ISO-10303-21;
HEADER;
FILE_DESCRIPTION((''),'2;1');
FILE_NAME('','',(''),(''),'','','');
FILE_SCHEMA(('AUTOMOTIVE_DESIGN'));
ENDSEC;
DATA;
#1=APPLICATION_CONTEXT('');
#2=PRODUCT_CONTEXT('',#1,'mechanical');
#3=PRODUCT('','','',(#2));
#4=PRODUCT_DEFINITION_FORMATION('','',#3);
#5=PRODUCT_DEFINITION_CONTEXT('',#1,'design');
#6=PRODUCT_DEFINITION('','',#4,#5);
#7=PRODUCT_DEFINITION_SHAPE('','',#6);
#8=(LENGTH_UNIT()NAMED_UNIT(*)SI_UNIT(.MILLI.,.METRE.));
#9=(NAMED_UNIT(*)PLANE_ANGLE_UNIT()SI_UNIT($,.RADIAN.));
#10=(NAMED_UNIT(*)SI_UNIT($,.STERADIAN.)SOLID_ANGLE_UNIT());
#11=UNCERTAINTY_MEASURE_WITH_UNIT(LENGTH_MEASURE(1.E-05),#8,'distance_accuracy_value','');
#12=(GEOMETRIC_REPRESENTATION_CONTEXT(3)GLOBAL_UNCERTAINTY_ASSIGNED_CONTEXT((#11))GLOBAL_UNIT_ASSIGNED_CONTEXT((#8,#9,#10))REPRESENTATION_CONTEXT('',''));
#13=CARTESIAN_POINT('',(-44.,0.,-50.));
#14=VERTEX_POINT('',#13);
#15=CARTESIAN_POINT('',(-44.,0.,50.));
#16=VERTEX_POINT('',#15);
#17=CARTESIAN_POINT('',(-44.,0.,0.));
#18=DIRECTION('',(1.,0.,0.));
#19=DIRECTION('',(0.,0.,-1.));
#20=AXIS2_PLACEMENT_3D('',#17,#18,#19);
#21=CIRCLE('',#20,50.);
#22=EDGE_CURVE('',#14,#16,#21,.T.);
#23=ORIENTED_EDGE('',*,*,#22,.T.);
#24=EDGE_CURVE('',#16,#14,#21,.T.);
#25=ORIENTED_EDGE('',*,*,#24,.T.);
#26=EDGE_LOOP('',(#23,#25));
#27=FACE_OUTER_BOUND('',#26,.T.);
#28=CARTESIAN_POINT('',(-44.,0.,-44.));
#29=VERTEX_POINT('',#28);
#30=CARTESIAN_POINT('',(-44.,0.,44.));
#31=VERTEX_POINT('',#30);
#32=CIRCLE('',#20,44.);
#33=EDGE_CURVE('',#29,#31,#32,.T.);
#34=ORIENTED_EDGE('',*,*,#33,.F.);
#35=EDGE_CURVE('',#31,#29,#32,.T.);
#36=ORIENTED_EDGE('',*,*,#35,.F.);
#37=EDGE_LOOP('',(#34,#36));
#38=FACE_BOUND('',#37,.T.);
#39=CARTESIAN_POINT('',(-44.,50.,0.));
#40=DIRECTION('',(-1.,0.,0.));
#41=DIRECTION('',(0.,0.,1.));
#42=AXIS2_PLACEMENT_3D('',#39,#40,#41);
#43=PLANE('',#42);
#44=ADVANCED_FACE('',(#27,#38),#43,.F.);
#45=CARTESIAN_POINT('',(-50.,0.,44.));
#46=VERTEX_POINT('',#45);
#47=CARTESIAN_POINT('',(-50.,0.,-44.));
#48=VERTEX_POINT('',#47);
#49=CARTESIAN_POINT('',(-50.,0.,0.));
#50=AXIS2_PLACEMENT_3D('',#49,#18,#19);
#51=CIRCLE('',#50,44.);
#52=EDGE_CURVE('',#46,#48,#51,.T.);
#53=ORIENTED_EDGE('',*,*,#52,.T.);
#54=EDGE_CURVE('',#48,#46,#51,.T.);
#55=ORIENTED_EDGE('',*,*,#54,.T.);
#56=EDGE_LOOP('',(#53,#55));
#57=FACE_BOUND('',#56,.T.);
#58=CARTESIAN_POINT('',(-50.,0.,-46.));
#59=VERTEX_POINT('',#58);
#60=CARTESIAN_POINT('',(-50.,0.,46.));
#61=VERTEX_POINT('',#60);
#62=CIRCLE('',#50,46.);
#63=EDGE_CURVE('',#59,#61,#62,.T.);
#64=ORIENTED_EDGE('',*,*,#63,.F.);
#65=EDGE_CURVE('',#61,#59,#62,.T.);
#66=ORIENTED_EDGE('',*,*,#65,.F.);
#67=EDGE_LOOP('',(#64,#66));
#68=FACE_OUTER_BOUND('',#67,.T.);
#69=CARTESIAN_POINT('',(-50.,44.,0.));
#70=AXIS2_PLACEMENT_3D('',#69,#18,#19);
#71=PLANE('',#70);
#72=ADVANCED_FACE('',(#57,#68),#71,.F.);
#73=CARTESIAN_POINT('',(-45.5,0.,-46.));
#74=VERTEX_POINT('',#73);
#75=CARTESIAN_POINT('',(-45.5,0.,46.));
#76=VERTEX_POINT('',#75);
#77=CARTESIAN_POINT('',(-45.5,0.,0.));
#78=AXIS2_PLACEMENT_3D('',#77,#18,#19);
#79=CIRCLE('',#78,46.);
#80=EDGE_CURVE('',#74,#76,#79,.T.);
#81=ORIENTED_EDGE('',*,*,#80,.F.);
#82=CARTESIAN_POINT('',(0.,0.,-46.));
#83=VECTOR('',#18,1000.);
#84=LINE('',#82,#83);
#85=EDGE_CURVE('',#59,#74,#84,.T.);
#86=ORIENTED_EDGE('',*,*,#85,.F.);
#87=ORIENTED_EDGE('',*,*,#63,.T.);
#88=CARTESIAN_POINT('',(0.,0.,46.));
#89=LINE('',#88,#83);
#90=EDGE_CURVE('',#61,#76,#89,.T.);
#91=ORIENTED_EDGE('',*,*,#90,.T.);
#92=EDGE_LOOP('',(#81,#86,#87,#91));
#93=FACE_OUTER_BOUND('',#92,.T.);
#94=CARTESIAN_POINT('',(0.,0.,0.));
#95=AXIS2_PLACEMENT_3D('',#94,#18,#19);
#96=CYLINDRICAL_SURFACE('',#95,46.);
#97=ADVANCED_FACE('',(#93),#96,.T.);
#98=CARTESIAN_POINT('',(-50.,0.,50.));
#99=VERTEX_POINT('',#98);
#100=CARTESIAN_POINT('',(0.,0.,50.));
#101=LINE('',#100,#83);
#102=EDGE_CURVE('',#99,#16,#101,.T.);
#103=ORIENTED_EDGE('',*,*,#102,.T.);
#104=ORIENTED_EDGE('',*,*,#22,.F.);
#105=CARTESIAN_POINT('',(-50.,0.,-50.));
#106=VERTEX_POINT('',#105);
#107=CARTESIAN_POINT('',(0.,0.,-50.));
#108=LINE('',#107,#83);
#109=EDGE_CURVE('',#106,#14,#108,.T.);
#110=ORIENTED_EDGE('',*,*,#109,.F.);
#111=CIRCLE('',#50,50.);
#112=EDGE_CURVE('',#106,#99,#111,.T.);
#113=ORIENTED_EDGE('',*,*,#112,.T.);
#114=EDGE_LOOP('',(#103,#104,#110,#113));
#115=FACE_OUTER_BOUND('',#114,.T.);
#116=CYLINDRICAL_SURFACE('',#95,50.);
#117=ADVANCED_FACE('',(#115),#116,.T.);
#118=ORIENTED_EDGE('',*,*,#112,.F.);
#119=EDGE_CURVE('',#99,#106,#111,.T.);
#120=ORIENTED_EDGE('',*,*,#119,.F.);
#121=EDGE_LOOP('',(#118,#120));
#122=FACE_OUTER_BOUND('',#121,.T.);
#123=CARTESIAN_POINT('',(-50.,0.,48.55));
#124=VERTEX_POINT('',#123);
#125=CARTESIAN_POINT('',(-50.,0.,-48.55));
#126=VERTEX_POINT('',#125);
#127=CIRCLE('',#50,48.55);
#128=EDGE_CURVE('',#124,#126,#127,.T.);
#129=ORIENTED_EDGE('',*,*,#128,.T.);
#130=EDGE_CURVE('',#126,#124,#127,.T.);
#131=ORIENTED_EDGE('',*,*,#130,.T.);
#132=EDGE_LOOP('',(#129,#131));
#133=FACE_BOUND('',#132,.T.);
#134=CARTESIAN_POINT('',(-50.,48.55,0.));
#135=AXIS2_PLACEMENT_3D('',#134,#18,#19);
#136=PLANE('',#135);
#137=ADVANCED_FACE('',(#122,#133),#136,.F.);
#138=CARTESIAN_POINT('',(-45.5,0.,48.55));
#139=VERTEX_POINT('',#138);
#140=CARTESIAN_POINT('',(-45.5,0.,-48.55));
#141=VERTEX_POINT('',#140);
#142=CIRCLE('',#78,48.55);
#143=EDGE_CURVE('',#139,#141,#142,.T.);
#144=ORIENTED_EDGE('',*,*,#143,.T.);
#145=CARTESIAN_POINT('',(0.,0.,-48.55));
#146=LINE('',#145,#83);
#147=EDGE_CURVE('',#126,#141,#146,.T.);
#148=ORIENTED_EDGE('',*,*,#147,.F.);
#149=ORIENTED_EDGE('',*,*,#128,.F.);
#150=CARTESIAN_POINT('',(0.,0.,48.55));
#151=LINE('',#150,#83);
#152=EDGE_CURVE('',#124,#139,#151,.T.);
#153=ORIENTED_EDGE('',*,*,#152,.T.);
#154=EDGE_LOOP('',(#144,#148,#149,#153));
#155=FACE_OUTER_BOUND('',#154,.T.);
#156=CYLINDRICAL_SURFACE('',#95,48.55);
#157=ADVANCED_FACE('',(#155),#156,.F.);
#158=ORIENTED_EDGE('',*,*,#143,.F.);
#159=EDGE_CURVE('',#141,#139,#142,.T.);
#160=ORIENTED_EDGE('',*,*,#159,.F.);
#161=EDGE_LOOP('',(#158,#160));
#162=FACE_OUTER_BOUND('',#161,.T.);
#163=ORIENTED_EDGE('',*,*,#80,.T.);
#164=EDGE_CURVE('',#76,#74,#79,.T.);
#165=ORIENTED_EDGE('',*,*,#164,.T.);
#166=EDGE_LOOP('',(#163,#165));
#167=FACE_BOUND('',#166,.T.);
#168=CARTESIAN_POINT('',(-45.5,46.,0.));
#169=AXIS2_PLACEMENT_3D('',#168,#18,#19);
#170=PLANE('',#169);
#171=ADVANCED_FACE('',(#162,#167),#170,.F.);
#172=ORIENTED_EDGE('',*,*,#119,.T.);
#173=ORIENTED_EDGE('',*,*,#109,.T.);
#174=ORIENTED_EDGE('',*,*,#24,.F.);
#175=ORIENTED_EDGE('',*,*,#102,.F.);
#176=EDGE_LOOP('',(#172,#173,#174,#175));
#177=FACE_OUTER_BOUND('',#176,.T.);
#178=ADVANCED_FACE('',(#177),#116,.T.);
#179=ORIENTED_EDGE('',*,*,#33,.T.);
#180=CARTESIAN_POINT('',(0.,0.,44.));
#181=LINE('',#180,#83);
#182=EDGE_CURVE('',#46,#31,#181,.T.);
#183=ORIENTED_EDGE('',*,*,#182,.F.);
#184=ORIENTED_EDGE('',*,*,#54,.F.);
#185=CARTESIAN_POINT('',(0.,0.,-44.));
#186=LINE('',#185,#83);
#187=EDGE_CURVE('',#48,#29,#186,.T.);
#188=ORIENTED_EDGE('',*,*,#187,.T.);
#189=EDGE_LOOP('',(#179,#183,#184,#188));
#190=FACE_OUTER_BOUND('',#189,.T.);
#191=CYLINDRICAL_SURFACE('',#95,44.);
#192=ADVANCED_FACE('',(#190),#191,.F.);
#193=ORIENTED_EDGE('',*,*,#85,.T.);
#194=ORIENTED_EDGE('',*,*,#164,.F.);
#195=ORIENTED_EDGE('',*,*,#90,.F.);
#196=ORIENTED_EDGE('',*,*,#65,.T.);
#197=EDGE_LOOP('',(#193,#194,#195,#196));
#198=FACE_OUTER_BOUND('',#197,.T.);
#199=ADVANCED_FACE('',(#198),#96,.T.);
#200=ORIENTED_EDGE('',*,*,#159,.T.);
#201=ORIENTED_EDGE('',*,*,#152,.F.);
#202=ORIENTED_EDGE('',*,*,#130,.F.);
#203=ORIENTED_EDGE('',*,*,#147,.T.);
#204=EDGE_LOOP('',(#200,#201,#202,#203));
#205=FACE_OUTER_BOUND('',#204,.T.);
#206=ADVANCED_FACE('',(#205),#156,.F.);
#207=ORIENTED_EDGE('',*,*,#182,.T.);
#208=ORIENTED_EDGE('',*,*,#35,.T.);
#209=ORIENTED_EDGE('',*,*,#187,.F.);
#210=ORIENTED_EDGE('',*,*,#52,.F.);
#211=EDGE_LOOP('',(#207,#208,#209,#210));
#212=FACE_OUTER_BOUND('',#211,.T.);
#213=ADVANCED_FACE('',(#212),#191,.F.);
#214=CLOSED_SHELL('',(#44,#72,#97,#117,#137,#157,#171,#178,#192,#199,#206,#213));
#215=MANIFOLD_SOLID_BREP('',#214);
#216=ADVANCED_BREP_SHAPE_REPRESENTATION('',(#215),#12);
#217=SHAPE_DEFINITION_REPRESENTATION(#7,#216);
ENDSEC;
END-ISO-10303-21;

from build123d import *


with BuildPart() as part:
    # Sketch1 → Revolve1 (revolve)
    with BuildSketch(Plane.XY, mode=Mode.PRIVATE) as revolve1_sk:
        Polygon((-50, 48.55), (-50, 50), (-44, 50), (-44, 44), (-50, 44), (-50, 46), (-45.5, 46), (-45.5, 48.55), align=None)
    revolve(revolve1_sk.sketch.rotate(Axis((0, 0, 0), (-1, 0, 0)), 90), axis=Axis((0, 0, 0), (-1, 0, 0)))


solid = part.part
